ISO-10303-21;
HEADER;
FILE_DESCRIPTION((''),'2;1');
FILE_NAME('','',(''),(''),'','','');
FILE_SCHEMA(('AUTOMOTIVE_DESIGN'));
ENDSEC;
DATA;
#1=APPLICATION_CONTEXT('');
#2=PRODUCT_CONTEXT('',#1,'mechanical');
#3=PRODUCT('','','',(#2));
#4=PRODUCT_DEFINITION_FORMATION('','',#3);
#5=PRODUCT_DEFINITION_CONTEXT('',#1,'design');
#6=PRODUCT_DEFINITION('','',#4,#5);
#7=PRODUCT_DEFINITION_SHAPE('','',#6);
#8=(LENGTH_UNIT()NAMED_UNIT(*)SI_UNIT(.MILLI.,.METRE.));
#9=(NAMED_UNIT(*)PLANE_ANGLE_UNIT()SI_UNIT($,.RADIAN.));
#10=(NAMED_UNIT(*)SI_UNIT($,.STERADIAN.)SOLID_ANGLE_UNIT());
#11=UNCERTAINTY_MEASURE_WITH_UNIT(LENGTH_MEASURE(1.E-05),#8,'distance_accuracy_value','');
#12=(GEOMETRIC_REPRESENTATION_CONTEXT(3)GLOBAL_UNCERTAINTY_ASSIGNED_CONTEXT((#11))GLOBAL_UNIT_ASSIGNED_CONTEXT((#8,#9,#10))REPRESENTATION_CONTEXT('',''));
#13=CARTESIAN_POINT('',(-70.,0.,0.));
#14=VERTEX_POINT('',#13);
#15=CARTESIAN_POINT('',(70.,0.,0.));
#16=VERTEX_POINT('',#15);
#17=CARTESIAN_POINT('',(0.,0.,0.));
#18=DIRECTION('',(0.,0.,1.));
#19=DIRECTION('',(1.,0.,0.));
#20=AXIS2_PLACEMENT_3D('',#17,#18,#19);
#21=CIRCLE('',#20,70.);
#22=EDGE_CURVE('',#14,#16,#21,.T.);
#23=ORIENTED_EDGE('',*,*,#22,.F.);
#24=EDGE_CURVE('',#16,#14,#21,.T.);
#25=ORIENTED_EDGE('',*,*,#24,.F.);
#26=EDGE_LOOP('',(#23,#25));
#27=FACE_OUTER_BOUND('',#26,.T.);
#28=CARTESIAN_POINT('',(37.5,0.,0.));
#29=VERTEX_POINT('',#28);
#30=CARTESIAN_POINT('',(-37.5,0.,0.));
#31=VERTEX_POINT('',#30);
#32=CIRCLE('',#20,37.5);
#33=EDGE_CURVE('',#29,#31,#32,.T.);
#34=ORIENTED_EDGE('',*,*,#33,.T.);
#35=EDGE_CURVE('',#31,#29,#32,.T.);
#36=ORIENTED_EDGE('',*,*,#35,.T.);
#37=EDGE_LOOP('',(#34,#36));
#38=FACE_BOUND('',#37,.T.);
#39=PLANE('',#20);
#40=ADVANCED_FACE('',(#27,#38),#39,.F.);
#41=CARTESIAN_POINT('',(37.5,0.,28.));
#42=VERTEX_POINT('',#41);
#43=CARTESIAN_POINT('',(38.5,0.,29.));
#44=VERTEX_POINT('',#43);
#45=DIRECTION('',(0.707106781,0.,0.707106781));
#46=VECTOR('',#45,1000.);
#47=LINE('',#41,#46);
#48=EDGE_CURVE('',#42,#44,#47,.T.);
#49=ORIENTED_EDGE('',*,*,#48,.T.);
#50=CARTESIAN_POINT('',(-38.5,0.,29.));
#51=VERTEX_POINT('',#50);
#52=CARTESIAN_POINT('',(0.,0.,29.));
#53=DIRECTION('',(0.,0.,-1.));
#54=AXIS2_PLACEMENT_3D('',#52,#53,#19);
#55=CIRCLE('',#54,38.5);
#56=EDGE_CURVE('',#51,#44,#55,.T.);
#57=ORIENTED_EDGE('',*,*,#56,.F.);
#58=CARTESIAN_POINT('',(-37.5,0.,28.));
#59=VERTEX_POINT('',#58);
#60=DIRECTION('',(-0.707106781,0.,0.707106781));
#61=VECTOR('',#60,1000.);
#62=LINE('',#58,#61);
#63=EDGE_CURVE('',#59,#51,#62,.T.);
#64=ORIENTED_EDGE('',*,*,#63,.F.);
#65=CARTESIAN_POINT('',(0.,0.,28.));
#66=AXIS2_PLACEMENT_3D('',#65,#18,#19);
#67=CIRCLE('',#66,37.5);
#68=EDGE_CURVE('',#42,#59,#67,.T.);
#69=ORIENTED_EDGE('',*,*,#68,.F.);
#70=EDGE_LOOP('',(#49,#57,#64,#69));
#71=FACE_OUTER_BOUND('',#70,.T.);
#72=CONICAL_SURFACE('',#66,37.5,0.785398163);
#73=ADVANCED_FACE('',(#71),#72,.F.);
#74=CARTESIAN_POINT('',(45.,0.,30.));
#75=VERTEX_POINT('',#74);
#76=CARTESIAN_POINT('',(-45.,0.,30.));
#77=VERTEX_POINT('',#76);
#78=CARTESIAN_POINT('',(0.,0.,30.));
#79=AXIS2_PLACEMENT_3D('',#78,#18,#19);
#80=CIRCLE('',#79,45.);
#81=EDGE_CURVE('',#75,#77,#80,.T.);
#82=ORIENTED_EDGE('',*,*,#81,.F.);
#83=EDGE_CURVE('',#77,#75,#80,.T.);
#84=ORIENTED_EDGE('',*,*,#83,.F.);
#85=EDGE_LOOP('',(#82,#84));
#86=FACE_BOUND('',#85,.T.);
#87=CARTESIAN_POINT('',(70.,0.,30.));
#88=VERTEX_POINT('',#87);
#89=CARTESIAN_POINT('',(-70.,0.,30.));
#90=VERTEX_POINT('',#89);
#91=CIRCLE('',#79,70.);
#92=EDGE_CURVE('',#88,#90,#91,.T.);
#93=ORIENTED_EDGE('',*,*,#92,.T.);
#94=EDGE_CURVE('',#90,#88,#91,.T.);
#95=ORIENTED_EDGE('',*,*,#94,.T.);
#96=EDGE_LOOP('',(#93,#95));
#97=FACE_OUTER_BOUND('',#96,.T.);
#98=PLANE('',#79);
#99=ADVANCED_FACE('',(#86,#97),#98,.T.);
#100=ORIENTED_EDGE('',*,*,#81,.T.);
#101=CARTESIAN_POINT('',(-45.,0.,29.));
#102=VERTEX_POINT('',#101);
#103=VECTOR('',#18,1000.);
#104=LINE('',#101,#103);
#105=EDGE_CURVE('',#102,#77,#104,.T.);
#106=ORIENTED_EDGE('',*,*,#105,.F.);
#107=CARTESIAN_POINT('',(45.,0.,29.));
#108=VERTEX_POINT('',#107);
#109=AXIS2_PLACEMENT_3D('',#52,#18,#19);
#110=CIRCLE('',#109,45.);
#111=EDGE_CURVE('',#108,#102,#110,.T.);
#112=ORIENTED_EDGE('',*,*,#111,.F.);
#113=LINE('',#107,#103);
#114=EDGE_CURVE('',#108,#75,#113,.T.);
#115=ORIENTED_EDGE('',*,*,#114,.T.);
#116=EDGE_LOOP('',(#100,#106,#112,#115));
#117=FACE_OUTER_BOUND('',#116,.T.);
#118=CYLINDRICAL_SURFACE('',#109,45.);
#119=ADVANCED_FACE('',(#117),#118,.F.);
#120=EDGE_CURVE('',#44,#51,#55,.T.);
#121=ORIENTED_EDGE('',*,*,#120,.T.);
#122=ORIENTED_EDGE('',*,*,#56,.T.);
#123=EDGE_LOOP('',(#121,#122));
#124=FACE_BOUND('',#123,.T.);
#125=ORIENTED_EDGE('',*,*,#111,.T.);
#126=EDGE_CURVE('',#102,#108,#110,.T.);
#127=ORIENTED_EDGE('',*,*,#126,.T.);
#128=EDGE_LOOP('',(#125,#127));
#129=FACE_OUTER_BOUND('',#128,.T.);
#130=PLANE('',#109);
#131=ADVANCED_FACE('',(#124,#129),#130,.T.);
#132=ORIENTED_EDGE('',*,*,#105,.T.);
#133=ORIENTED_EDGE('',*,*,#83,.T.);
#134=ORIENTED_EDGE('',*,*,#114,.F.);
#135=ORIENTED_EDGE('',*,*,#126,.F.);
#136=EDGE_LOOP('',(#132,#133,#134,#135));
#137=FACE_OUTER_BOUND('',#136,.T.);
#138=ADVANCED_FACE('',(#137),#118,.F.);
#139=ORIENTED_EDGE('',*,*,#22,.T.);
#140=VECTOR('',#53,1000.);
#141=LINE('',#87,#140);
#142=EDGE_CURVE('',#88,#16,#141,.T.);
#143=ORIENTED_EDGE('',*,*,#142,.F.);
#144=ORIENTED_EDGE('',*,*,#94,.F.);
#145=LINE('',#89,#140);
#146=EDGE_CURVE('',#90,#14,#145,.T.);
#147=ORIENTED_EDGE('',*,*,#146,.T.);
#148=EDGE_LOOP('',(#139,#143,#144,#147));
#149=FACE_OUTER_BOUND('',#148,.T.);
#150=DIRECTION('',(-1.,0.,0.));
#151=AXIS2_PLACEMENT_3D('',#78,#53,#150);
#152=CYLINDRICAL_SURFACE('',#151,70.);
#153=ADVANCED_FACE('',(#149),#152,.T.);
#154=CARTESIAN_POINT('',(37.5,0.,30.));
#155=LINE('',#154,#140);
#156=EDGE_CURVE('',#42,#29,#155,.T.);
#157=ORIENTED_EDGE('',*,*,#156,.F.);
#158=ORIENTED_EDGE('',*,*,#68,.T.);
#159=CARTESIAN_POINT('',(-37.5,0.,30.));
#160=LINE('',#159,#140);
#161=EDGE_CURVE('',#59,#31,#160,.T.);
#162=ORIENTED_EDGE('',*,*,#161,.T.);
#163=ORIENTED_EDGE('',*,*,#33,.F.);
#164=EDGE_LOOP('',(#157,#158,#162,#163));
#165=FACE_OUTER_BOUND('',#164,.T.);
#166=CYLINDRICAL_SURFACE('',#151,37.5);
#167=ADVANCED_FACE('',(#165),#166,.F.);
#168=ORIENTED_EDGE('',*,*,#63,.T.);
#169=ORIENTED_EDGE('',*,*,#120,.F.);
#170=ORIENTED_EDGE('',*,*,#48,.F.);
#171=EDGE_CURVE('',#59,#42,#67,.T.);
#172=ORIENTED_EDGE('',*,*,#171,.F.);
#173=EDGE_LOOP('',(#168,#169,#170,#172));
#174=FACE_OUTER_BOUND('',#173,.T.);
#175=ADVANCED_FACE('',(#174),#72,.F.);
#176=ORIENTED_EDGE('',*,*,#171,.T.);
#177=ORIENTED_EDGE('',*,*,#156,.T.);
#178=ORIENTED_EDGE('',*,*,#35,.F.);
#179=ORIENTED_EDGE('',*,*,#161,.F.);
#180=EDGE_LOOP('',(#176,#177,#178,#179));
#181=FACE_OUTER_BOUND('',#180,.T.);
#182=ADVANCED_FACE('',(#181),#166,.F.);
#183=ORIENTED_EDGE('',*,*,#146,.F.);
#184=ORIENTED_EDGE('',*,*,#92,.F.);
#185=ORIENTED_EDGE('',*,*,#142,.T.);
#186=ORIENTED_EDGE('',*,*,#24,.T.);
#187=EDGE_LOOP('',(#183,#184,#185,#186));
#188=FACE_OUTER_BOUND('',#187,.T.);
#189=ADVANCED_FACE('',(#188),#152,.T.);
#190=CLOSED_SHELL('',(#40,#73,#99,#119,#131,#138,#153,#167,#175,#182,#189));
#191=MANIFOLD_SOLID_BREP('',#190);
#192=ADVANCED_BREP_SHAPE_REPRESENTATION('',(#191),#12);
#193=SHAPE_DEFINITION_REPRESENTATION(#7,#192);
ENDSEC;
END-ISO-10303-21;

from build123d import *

# Parameters (mm, degrees)
SKETCH_1_R          = 70
SKETCH_1_R_2        = 37.5
EXTRUDE_1_DEPTH     = 30
SKETCH_2_R          = 45
CUT_EXTRUDE_1_DEPTH = 1
CHAMFER_1_SIZE      = 1


with BuildPart() as part:
    # 草图1 → 凸台-拉伸1 (new body)
    with BuildSketch(Plane.XY):
        Circle(SKETCH_1_R)
        Circle(SKETCH_1_R_2, mode=Mode.SUBTRACT)
    extrude(amount=EXTRUDE_1_DEPTH)

    # 草图2 → 切除-拉伸1 (cut)
    with BuildSketch(Plane.XY.offset(30)):
        Circle(SKETCH_2_R)
    extrude(amount=-CUT_EXTRUDE_1_DEPTH, mode=Mode.SUBTRACT)

    # 倒角1
    chamfer_1_edges = [part.edges().sort_by_distance(p)[0] for p in [
        (-37.5, 0, 29),
    ]]
    chamfer(chamfer_1_edges, length=CHAMFER_1_SIZE)


solid = part.part
